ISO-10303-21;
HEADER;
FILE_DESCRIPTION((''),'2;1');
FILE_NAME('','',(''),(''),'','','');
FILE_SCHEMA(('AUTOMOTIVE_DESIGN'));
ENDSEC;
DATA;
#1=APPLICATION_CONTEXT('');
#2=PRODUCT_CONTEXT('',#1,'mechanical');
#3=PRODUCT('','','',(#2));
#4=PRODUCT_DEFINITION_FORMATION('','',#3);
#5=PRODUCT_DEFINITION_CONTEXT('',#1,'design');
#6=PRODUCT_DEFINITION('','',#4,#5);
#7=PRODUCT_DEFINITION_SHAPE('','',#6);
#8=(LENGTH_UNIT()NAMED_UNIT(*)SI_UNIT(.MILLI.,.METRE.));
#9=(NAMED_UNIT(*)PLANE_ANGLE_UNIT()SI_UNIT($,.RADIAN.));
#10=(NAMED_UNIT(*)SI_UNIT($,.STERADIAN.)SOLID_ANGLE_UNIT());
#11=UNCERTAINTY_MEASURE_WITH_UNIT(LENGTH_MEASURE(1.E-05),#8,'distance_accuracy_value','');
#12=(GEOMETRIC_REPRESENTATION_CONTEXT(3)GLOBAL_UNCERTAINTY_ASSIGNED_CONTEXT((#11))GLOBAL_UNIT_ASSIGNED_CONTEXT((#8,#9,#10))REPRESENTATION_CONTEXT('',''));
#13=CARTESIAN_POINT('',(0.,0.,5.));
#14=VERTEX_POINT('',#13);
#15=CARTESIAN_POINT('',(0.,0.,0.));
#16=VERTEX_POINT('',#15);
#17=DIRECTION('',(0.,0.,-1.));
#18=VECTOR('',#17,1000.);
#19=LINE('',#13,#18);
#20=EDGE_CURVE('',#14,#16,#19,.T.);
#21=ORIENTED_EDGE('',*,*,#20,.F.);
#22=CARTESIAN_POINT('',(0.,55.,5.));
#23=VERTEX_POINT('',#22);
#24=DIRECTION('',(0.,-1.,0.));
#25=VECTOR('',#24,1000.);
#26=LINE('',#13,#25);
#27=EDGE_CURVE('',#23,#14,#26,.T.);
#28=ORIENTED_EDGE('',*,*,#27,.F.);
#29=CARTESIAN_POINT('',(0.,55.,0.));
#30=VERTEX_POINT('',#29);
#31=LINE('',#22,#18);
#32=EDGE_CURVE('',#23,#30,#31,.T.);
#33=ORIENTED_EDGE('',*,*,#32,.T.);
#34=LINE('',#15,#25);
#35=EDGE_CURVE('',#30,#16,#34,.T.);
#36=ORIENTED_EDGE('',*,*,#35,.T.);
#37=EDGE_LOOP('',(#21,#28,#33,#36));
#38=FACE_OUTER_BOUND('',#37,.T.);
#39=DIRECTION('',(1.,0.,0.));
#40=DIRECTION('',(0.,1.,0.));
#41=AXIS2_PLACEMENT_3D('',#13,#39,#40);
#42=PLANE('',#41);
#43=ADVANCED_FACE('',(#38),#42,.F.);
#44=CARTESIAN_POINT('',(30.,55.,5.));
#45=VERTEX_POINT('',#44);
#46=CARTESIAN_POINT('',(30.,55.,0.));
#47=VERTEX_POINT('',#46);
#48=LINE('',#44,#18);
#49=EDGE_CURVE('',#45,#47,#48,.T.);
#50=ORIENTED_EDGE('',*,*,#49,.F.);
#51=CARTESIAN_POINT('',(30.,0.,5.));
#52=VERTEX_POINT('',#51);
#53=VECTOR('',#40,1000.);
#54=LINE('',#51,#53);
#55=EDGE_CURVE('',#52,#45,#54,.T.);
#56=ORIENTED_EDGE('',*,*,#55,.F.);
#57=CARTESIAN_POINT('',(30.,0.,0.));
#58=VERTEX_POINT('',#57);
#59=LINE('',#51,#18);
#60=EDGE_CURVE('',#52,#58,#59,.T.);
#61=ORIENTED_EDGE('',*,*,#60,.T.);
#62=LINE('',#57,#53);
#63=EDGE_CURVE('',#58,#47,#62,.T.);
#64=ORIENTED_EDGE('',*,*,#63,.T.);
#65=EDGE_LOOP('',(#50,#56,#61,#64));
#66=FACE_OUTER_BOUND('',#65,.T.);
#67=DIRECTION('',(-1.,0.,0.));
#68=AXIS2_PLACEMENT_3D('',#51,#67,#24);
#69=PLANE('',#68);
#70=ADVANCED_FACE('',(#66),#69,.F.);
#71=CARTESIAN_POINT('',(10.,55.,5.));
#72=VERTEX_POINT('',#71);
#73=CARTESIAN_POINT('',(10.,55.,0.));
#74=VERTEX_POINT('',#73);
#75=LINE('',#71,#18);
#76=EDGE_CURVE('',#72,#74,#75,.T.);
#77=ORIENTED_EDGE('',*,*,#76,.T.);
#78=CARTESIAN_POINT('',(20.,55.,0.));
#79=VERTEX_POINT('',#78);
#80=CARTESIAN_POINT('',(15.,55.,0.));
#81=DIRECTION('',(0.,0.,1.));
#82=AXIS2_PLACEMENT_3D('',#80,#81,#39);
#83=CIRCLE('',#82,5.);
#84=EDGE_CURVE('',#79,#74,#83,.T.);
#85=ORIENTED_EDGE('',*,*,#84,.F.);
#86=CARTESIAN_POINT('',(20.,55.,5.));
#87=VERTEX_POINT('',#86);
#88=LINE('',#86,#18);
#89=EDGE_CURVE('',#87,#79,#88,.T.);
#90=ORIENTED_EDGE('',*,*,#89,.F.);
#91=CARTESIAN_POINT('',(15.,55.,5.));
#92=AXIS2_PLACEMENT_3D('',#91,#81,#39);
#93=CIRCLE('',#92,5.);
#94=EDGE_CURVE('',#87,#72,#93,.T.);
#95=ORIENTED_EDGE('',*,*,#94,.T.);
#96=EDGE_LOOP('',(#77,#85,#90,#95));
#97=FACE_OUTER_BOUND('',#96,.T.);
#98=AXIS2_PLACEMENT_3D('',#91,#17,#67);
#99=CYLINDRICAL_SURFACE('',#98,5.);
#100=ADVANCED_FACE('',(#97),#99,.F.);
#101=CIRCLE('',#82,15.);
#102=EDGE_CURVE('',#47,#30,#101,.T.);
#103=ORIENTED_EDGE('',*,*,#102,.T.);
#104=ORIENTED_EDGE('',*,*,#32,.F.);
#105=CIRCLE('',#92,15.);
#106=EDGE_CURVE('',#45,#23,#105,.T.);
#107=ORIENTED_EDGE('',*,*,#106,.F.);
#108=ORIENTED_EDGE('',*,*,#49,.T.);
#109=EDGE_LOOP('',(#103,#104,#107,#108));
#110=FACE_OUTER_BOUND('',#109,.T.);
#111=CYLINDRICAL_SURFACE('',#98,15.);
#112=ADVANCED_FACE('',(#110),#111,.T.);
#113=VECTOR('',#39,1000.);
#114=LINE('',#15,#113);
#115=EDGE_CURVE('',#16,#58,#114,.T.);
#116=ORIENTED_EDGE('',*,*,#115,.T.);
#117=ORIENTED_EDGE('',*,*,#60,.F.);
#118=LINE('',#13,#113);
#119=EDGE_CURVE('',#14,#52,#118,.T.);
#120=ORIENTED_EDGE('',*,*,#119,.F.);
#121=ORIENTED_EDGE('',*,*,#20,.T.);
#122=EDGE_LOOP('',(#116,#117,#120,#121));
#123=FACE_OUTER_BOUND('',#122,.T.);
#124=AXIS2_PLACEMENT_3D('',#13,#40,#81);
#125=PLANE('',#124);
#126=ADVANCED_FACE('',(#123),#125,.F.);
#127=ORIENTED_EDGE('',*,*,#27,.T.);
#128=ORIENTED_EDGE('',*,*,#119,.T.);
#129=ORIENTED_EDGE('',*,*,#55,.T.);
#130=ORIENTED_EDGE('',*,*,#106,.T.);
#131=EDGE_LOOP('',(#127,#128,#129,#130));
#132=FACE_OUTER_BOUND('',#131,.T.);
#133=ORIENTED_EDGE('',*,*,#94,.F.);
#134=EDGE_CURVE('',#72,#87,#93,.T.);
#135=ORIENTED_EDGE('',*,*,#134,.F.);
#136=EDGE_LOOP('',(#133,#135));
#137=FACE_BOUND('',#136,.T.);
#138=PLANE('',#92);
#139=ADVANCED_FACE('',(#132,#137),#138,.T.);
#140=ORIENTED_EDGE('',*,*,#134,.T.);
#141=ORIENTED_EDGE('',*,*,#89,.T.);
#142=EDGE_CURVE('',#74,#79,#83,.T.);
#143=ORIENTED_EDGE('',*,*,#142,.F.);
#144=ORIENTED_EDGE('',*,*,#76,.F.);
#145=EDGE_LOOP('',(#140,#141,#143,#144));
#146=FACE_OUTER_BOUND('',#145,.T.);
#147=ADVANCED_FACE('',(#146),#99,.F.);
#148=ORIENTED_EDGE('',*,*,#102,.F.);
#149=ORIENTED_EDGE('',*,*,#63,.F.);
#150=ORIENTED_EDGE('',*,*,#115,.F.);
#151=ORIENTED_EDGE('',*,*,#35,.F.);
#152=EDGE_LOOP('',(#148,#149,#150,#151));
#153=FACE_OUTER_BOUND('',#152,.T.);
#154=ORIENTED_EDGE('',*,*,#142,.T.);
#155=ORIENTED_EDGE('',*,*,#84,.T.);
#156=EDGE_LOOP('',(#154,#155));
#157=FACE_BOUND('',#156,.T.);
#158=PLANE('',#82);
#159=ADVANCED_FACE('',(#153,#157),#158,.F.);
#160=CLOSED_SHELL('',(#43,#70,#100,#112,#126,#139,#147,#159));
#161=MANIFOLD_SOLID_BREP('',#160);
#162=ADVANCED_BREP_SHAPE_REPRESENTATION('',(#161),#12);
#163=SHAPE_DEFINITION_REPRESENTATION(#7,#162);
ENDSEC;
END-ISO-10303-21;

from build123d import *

# Parameters (mm, degrees)
SKETCH_1_R      = 5
EXTRUDE_1_DEPTH = 5


with BuildPart() as part:
    # 草图1 → 凸台-拉伸1 (new body)
    with BuildSketch(Plane.XY):
        with BuildLine():
            Line((0, 0), (30, 0))
            Line((30, 0), (30, 55))
            ThreePointArc((30, 55), (15, 70), (0, 55))
            Line((0, 55), (0, 0))
        make_face()
        with Locations((15, 55)):
            Circle(SKETCH_1_R, mode=Mode.SUBTRACT)
    extrude(amount=EXTRUDE_1_DEPTH)


solid = part.part
